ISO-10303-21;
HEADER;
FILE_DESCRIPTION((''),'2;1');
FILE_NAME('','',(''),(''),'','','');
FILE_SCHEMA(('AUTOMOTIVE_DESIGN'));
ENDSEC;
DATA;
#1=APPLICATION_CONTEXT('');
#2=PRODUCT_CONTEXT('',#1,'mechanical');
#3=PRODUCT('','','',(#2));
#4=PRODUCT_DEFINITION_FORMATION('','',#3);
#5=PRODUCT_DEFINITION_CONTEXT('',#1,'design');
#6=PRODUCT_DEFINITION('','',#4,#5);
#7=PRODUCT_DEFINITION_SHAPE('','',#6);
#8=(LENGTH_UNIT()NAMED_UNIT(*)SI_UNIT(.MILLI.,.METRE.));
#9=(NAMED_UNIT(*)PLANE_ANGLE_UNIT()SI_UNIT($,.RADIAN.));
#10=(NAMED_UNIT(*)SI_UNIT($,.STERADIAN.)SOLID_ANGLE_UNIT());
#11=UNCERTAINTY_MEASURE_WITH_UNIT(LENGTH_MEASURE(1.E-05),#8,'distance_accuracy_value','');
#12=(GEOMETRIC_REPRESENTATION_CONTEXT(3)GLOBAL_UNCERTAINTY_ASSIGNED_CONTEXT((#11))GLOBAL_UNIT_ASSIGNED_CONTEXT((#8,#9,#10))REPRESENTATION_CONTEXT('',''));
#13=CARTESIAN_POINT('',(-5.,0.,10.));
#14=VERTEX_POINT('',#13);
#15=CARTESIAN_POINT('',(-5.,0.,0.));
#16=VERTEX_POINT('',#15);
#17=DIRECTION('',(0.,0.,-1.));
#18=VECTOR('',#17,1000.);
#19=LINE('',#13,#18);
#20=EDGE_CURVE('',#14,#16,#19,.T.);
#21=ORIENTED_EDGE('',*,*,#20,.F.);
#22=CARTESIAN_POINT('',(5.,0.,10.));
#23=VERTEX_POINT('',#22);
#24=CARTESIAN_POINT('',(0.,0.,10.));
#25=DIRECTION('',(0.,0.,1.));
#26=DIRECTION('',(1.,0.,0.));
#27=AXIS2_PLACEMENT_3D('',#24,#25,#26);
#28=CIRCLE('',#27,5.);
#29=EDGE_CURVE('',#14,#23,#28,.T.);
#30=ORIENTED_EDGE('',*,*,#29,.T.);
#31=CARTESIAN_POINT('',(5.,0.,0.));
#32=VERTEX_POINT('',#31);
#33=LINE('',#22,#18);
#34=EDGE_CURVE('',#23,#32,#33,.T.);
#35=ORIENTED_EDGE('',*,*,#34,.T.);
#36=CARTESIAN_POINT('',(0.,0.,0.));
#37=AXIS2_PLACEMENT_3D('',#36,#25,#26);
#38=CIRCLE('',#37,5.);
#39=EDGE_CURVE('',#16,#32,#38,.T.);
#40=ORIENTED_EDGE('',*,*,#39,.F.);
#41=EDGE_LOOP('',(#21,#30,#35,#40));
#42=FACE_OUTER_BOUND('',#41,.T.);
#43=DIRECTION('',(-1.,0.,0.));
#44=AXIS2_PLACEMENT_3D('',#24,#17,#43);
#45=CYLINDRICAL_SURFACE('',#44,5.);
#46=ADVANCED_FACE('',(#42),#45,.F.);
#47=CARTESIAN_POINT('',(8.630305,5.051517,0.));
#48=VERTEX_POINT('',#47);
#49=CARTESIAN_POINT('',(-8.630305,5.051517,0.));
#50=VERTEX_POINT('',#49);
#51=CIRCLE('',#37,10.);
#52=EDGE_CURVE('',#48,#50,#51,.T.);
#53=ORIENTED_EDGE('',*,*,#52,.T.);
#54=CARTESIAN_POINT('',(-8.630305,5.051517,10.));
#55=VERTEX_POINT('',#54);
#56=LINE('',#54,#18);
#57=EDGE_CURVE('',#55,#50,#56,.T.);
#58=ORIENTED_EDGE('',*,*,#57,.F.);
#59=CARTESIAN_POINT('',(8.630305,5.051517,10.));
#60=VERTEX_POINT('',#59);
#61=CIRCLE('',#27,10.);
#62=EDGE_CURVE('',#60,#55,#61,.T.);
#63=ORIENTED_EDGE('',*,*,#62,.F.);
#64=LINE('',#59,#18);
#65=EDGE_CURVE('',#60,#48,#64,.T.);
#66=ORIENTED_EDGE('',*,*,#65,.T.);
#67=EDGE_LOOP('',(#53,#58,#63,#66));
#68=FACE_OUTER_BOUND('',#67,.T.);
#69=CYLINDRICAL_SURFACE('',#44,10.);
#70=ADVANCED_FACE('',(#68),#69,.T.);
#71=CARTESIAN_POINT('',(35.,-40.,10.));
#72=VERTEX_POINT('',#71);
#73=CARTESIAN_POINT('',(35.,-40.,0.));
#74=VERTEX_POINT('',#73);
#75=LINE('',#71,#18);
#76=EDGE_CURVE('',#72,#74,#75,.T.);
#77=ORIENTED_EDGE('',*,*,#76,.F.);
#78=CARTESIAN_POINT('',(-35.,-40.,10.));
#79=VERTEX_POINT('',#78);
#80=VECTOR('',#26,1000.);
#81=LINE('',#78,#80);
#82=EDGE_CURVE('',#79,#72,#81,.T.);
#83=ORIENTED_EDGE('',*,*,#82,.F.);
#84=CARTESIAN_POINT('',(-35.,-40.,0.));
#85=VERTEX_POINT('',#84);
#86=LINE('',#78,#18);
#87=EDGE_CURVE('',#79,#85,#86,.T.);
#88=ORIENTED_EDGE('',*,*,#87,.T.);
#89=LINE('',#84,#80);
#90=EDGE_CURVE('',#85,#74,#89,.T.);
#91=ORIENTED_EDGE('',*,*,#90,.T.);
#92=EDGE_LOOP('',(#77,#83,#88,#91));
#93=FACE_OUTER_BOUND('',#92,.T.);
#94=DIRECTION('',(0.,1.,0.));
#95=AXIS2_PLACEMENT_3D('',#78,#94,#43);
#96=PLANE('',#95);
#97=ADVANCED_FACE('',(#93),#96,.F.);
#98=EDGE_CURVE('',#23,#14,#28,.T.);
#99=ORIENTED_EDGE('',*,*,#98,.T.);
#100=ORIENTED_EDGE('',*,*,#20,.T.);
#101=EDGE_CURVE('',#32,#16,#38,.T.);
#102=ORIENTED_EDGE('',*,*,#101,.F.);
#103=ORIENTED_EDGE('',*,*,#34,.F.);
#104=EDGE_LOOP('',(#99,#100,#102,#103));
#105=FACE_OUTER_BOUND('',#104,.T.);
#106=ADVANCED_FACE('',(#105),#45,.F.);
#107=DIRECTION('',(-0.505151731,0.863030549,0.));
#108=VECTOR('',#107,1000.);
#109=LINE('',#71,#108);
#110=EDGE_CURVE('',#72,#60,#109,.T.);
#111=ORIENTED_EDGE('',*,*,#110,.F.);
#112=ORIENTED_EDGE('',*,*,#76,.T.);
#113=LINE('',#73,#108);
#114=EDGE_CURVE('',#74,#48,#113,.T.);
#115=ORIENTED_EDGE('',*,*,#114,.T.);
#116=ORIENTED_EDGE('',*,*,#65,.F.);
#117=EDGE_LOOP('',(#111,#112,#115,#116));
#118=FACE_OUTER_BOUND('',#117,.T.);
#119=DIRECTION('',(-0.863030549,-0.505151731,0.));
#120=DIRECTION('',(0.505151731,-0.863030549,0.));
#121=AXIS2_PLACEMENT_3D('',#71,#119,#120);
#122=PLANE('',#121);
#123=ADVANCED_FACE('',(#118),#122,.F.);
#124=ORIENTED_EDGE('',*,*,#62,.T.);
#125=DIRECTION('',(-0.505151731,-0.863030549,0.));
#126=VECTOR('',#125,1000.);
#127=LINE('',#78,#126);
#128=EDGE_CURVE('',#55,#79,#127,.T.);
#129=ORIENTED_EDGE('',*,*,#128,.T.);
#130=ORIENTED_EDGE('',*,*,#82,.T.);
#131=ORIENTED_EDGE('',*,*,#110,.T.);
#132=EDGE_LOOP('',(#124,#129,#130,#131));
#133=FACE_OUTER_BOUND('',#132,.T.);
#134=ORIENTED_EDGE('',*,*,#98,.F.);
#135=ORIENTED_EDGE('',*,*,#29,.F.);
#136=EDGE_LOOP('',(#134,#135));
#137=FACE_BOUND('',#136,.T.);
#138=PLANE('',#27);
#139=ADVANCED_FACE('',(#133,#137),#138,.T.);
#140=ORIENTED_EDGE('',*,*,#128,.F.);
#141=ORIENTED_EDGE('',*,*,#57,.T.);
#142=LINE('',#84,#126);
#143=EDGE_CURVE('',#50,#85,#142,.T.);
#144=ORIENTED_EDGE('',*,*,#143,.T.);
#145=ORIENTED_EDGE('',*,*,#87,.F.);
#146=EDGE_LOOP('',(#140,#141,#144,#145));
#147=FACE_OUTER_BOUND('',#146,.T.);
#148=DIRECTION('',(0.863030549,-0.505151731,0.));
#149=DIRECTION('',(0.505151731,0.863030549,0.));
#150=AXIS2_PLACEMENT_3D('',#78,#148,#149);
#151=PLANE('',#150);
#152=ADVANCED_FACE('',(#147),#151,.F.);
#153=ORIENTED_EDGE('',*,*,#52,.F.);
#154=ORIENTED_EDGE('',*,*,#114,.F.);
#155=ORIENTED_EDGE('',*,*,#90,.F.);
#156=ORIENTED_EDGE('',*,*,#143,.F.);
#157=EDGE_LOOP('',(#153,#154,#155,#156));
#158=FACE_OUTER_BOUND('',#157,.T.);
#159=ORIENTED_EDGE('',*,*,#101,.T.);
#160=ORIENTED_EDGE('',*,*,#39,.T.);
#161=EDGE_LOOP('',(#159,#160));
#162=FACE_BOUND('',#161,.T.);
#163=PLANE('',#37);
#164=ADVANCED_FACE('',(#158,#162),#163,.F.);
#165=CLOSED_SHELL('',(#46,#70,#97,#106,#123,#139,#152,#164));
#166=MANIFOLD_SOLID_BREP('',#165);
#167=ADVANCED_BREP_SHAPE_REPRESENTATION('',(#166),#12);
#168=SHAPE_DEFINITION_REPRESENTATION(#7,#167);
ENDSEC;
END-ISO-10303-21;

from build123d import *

# Parameters (mm, degrees)
SKETCH1_R           = 5
BOSS_EXTRUDE1_DEPTH = 10


with BuildPart() as part:
    # Sketch1 → Boss-Extrude1 (new body)
    with BuildSketch(Plane.XY):
        with BuildLine():
            Line((-35, -40), (35, -40))
            Line((35, -40), (8.630305493, 5.051517306))
            ThreePointArc((8.630305493, 5.051517306), (0, 10), (-8.630305493, 5.051517306))
            Line((-8.630305493, 5.051517306), (-35, -40))
        make_face()
        Circle(SKETCH1_R, mode=Mode.SUBTRACT)
    extrude(amount=BOSS_EXTRUDE1_DEPTH)


solid = part.part
